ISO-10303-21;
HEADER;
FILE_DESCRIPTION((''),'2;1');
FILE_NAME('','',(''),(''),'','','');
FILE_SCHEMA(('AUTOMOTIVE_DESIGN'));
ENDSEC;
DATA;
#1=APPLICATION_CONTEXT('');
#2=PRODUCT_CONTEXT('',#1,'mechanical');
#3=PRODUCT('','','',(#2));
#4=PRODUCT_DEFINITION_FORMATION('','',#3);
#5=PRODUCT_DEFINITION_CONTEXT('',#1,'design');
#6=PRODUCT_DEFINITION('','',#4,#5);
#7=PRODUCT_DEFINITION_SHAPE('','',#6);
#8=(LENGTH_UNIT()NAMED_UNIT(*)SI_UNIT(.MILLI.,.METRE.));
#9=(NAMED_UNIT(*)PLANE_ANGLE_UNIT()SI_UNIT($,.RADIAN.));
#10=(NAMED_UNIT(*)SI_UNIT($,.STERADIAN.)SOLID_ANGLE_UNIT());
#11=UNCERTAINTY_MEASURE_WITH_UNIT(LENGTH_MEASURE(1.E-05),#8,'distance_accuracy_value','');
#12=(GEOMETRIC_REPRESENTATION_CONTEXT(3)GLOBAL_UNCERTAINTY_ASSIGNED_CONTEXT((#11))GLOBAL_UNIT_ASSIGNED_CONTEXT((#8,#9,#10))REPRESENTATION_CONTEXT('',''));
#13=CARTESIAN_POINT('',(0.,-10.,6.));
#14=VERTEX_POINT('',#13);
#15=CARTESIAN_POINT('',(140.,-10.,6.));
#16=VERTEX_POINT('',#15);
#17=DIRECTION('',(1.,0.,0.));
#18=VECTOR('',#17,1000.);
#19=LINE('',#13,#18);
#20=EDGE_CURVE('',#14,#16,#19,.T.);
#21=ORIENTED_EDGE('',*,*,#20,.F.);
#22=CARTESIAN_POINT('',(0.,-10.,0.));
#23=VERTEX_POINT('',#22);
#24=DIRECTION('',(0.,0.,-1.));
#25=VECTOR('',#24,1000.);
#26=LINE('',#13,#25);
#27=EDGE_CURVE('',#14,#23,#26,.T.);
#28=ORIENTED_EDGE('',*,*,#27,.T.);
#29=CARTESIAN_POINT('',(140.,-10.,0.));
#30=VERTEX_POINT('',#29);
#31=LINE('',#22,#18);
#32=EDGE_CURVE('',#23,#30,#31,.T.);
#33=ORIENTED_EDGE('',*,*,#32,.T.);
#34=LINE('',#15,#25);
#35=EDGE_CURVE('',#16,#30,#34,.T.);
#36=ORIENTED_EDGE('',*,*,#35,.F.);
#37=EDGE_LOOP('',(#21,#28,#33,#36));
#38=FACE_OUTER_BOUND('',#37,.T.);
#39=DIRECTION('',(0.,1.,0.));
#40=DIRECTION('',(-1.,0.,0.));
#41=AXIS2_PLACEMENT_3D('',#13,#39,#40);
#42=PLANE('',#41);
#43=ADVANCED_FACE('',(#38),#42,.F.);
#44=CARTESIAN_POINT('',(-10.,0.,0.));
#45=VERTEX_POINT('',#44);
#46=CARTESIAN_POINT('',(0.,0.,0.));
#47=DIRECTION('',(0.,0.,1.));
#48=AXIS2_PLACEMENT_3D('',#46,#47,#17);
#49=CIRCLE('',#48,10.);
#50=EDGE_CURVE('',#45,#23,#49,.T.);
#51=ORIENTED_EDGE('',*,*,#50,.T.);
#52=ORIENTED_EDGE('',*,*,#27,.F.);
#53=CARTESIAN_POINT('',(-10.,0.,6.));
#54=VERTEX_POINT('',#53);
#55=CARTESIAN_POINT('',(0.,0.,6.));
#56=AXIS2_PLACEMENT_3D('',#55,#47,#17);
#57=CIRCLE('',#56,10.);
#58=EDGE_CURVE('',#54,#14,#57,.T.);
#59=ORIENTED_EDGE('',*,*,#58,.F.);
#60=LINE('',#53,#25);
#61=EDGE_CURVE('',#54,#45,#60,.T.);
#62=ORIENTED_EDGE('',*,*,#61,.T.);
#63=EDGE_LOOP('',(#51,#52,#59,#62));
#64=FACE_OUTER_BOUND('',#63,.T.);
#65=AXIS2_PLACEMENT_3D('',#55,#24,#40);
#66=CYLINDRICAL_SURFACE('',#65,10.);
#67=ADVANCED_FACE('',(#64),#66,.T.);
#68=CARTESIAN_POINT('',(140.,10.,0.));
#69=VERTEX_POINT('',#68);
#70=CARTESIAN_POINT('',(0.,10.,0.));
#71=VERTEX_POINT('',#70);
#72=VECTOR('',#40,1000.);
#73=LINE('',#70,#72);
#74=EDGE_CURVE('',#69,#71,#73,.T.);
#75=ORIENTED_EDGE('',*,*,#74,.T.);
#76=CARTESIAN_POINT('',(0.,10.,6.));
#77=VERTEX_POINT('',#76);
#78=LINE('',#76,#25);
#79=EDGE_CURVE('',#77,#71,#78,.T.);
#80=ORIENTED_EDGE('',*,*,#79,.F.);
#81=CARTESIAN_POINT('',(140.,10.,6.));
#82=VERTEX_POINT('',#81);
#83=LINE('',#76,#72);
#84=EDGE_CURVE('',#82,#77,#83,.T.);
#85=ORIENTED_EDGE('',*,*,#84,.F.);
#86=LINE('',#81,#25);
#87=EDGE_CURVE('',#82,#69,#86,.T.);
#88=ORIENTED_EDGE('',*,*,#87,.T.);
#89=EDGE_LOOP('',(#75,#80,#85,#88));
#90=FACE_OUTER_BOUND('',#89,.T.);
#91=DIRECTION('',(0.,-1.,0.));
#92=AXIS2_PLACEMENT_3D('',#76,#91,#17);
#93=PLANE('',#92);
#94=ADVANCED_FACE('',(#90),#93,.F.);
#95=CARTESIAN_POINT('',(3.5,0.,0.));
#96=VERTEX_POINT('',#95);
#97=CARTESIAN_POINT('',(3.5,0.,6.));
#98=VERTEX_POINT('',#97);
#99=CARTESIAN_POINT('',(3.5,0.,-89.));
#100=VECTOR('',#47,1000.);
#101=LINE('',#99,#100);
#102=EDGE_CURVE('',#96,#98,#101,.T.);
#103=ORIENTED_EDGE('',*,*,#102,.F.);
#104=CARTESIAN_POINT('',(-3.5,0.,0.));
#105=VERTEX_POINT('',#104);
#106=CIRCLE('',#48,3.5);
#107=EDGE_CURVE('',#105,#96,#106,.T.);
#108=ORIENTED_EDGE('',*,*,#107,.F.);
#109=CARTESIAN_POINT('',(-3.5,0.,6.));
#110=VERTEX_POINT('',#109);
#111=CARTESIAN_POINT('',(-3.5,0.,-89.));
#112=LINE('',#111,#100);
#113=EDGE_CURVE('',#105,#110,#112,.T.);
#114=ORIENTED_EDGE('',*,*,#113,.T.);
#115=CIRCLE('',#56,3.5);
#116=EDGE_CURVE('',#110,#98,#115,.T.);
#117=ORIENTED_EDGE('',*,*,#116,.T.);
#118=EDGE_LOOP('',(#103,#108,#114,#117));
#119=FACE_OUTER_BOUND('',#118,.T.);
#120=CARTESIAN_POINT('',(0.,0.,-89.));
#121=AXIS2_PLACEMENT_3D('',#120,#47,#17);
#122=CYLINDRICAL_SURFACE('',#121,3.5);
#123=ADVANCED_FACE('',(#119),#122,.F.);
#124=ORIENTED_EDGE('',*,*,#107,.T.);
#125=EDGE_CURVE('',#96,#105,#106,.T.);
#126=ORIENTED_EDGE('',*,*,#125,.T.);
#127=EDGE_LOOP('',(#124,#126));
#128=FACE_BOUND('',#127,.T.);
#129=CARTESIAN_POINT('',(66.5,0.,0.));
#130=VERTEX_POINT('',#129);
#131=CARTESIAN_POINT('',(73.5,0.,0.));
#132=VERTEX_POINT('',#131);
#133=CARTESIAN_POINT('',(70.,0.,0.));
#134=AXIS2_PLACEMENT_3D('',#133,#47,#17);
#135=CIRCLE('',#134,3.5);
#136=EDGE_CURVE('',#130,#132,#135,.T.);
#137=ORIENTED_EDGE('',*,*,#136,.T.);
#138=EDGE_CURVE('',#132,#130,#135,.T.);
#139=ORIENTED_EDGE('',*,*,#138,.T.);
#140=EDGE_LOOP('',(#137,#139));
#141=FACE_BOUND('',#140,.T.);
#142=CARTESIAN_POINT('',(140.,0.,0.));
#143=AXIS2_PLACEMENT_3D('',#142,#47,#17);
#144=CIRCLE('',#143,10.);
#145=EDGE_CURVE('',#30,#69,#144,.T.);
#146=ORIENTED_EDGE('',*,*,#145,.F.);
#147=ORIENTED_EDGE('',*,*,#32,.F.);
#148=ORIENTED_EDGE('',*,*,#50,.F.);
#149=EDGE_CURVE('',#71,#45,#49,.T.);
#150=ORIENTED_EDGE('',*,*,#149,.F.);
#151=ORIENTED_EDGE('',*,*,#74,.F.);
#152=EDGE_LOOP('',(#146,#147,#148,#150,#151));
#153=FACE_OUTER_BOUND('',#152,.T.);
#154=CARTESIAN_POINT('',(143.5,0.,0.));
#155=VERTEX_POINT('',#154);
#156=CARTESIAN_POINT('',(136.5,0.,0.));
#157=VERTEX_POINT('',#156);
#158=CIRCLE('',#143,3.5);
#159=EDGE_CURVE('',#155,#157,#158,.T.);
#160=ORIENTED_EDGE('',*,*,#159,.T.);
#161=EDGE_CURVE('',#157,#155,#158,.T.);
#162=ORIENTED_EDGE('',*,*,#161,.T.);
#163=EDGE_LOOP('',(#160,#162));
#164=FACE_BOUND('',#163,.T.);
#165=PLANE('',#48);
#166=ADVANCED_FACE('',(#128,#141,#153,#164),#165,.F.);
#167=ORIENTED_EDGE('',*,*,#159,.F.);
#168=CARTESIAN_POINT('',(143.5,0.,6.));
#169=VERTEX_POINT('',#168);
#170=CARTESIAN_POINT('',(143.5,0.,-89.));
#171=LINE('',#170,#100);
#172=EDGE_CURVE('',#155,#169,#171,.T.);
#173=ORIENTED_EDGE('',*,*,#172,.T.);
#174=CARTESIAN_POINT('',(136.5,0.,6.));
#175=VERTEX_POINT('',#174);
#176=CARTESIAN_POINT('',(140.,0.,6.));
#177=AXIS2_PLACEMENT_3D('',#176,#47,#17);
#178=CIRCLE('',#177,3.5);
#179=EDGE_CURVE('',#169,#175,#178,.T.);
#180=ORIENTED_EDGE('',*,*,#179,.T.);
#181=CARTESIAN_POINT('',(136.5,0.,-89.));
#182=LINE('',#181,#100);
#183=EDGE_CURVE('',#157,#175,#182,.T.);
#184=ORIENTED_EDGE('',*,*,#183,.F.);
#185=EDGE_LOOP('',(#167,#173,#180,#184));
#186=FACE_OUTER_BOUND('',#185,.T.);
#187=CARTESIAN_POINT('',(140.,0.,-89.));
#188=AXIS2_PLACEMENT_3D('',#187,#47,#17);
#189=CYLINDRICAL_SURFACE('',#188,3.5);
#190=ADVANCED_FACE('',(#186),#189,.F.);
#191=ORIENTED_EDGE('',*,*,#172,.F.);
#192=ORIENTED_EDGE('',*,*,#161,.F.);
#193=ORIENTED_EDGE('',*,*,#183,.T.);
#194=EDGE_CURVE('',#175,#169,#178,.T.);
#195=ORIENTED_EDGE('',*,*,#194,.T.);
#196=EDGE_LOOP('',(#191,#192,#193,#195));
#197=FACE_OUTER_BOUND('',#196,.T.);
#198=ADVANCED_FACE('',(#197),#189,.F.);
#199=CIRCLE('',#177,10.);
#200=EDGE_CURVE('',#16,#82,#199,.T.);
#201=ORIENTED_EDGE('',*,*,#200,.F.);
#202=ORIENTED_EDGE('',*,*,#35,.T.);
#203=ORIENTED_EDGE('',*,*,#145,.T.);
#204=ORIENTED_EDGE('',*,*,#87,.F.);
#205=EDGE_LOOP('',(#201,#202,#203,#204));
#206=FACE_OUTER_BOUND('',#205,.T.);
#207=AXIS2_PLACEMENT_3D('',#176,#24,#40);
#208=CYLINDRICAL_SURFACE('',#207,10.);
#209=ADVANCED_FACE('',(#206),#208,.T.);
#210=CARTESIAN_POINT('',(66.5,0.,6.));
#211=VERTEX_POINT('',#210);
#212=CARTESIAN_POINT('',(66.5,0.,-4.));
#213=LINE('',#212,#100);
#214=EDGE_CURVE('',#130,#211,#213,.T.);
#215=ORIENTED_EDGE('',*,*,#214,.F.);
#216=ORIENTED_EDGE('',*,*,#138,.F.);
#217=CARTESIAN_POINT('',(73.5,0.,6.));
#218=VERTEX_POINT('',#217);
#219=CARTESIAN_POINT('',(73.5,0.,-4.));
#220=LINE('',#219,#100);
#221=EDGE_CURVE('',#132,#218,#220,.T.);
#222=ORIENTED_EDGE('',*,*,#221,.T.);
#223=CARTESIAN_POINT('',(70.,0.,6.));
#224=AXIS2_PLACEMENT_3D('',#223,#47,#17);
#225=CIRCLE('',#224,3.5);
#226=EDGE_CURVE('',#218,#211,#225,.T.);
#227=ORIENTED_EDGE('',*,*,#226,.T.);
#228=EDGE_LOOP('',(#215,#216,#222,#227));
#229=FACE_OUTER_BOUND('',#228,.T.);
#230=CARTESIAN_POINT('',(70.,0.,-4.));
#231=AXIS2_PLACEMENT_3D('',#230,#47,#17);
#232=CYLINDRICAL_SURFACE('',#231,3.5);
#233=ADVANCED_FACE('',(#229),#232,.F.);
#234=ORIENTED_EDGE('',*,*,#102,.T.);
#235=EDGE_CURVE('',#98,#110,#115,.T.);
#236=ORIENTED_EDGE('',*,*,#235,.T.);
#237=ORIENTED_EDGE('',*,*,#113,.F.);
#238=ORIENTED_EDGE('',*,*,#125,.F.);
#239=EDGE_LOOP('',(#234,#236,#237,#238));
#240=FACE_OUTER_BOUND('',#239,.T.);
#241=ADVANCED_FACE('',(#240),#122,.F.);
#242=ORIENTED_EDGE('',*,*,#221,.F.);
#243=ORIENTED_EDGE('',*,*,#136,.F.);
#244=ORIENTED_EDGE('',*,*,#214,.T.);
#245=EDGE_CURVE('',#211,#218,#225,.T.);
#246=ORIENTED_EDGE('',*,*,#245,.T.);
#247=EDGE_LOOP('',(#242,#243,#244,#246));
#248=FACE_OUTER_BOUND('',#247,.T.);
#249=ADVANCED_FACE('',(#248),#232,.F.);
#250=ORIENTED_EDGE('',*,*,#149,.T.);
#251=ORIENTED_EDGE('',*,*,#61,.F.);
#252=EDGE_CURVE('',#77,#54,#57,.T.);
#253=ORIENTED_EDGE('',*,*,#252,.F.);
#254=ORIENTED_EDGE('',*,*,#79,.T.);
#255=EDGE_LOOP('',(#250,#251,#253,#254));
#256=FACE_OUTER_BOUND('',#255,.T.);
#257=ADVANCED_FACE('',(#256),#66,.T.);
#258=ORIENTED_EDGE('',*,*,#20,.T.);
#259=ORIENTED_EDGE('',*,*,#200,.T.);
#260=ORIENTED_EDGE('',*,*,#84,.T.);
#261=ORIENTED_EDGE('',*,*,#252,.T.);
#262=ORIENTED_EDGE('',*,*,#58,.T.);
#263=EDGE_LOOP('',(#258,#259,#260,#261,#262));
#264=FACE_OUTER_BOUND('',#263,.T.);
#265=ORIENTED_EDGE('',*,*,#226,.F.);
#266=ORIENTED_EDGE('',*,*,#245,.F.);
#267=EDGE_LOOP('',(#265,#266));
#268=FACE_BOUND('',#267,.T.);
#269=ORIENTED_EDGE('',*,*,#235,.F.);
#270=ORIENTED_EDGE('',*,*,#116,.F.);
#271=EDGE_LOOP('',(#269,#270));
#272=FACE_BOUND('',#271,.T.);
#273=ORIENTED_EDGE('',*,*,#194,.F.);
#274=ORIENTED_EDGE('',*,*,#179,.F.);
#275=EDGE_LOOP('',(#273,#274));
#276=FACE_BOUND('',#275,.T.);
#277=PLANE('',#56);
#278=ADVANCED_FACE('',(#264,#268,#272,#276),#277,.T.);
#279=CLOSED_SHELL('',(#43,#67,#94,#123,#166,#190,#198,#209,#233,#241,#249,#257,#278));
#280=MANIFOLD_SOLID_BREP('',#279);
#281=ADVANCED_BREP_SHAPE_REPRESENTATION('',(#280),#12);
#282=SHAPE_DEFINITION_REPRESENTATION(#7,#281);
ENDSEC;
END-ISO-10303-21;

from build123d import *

# Parameters (mm, degrees)
BOSS_EXTRUDE1_DEPTH = 6
SKETCH2_R           = 3.5
CUT_EXTRUDE1_DEPTH  = 95
SKETCH3_R           = 3.5
CUT_EXTRUDE2_DEPTH  = 10


with BuildPart() as part:
    # Sketch1 → Boss-Extrude1 (new body)
    with BuildSketch(Plane.XY):
        with BuildLine():
            Line((0, 10), (140, 10))
            ThreePointArc((140, 10), (150, 0), (140, -10))
            Line((140, -10), (0, -10))
            ThreePointArc((0, -10), (-10, 0), (0, 10))
        make_face()
    extrude(amount=BOSS_EXTRUDE1_DEPTH)

    # Sketch2 → Cut-Extrude1 (cut)
    with BuildSketch(Plane.XY.offset(6)):
        Circle(SKETCH2_R)
        with Locations((140, 0)):
            Circle(SKETCH2_R)
    extrude(amount=-CUT_EXTRUDE1_DEPTH, mode=Mode.SUBTRACT)

    # Sketch3 → Cut-Extrude2 (cut)
    with BuildSketch(Plane.XY.offset(6)):
        with Locations((70, 0)):
            Circle(SKETCH3_R)
    extrude(amount=-CUT_EXTRUDE2_DEPTH, mode=Mode.SUBTRACT)


solid = part.part
